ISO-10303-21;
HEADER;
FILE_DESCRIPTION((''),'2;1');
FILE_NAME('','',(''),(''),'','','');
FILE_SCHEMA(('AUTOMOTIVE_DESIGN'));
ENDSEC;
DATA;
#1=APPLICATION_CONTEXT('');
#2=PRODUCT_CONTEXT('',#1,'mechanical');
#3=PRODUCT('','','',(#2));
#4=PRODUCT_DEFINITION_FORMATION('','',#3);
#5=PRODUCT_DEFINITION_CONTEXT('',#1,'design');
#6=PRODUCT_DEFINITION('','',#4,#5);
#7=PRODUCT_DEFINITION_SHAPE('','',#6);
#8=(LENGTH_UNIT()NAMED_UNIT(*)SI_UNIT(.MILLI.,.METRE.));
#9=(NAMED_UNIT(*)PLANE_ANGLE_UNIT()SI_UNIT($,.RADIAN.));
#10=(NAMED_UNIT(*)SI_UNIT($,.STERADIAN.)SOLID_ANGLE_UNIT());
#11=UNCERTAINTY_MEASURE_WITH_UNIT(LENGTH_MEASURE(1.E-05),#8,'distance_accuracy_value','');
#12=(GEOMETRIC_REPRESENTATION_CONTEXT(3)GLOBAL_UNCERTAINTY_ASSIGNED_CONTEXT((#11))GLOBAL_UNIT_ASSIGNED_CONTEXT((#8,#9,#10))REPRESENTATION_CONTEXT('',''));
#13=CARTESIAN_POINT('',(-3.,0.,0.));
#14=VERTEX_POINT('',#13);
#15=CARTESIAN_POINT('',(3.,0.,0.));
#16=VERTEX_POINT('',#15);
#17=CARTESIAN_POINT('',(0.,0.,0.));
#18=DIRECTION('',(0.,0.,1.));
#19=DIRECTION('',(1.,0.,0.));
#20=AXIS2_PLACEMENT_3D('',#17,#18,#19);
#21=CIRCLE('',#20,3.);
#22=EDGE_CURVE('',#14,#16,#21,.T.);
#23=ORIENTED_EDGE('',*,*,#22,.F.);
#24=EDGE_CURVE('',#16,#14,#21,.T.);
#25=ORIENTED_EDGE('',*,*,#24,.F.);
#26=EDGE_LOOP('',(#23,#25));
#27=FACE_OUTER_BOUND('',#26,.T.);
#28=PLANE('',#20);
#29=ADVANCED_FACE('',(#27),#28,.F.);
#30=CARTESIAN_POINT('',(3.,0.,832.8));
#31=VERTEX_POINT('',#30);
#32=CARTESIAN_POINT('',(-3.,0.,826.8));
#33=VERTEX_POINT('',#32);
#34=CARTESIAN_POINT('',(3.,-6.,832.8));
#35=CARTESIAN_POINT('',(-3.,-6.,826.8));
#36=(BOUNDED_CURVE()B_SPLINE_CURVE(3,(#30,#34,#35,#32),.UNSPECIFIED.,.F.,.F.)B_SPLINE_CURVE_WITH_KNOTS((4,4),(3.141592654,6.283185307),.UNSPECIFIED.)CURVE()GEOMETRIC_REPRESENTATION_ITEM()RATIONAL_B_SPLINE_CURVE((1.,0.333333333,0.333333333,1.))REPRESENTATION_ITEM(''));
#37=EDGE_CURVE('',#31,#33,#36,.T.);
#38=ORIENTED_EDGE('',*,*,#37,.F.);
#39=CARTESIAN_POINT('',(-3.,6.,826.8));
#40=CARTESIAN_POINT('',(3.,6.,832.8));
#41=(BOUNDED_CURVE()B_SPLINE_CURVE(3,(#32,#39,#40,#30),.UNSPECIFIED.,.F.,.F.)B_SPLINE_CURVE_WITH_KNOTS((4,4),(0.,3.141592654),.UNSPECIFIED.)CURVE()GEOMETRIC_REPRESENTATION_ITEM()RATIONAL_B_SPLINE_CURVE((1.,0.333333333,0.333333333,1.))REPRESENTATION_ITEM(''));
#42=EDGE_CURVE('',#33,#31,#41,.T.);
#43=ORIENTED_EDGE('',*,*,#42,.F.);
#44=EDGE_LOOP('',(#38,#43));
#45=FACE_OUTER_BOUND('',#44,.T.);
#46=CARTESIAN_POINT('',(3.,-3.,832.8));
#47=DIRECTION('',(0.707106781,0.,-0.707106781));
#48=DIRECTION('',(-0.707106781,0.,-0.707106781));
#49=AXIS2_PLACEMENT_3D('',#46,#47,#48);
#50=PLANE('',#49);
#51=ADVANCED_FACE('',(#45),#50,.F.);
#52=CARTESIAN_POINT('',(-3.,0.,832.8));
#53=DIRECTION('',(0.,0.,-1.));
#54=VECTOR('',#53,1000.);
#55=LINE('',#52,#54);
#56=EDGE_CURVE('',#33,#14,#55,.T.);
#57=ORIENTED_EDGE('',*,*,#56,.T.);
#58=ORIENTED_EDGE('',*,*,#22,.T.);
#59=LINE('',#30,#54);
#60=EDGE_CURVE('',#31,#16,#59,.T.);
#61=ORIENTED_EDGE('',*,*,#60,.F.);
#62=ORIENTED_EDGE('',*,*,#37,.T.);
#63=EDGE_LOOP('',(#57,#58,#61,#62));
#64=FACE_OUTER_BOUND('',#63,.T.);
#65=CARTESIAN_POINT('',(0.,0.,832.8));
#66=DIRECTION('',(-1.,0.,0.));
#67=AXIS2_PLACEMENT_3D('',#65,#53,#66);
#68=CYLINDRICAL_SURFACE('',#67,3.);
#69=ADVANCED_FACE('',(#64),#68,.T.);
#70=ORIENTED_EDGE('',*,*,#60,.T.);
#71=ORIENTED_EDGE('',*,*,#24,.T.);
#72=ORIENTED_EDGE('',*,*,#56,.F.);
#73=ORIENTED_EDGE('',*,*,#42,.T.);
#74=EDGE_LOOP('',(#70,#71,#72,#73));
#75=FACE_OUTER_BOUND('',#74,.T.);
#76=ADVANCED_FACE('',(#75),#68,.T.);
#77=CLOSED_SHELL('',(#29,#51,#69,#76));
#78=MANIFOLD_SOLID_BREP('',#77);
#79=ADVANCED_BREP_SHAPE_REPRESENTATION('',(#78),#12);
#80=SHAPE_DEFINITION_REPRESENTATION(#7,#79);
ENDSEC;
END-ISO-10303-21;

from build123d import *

# Parameters (mm, degrees)
SKETCH1_R               = 3
BOSS_EXTRUDE1_DEPTH     = 832.8
CUT_EXTRUDE1_DEPTH      = 833.810806846
CUT_EXTRUDE1_DEPTH_BACK = 833.810806846


with BuildPart() as part:
    # Sketch1 → Boss-Extrude1 (new body)
    with BuildSketch(Plane.XY):
        Circle(SKETCH1_R)
    extrude(amount=BOSS_EXTRUDE1_DEPTH)

    # Sketch2 → Cut-Extrude1 (cut, two sides: drawn at the far end of the back side and taken through both)
    with BuildSketch(Plane(origin=(0, 0, 0), x_dir=(1, 0, 0), z_dir=(0, 1, 0)).offset(-CUT_EXTRUDE1_DEPTH_BACK)):
        Polygon((3, -832.8), (-3, -826.8), (-3, -832.8), align=None)
    extrude(amount=CUT_EXTRUDE1_DEPTH + CUT_EXTRUDE1_DEPTH_BACK, mode=Mode.SUBTRACT)


solid = part.part
